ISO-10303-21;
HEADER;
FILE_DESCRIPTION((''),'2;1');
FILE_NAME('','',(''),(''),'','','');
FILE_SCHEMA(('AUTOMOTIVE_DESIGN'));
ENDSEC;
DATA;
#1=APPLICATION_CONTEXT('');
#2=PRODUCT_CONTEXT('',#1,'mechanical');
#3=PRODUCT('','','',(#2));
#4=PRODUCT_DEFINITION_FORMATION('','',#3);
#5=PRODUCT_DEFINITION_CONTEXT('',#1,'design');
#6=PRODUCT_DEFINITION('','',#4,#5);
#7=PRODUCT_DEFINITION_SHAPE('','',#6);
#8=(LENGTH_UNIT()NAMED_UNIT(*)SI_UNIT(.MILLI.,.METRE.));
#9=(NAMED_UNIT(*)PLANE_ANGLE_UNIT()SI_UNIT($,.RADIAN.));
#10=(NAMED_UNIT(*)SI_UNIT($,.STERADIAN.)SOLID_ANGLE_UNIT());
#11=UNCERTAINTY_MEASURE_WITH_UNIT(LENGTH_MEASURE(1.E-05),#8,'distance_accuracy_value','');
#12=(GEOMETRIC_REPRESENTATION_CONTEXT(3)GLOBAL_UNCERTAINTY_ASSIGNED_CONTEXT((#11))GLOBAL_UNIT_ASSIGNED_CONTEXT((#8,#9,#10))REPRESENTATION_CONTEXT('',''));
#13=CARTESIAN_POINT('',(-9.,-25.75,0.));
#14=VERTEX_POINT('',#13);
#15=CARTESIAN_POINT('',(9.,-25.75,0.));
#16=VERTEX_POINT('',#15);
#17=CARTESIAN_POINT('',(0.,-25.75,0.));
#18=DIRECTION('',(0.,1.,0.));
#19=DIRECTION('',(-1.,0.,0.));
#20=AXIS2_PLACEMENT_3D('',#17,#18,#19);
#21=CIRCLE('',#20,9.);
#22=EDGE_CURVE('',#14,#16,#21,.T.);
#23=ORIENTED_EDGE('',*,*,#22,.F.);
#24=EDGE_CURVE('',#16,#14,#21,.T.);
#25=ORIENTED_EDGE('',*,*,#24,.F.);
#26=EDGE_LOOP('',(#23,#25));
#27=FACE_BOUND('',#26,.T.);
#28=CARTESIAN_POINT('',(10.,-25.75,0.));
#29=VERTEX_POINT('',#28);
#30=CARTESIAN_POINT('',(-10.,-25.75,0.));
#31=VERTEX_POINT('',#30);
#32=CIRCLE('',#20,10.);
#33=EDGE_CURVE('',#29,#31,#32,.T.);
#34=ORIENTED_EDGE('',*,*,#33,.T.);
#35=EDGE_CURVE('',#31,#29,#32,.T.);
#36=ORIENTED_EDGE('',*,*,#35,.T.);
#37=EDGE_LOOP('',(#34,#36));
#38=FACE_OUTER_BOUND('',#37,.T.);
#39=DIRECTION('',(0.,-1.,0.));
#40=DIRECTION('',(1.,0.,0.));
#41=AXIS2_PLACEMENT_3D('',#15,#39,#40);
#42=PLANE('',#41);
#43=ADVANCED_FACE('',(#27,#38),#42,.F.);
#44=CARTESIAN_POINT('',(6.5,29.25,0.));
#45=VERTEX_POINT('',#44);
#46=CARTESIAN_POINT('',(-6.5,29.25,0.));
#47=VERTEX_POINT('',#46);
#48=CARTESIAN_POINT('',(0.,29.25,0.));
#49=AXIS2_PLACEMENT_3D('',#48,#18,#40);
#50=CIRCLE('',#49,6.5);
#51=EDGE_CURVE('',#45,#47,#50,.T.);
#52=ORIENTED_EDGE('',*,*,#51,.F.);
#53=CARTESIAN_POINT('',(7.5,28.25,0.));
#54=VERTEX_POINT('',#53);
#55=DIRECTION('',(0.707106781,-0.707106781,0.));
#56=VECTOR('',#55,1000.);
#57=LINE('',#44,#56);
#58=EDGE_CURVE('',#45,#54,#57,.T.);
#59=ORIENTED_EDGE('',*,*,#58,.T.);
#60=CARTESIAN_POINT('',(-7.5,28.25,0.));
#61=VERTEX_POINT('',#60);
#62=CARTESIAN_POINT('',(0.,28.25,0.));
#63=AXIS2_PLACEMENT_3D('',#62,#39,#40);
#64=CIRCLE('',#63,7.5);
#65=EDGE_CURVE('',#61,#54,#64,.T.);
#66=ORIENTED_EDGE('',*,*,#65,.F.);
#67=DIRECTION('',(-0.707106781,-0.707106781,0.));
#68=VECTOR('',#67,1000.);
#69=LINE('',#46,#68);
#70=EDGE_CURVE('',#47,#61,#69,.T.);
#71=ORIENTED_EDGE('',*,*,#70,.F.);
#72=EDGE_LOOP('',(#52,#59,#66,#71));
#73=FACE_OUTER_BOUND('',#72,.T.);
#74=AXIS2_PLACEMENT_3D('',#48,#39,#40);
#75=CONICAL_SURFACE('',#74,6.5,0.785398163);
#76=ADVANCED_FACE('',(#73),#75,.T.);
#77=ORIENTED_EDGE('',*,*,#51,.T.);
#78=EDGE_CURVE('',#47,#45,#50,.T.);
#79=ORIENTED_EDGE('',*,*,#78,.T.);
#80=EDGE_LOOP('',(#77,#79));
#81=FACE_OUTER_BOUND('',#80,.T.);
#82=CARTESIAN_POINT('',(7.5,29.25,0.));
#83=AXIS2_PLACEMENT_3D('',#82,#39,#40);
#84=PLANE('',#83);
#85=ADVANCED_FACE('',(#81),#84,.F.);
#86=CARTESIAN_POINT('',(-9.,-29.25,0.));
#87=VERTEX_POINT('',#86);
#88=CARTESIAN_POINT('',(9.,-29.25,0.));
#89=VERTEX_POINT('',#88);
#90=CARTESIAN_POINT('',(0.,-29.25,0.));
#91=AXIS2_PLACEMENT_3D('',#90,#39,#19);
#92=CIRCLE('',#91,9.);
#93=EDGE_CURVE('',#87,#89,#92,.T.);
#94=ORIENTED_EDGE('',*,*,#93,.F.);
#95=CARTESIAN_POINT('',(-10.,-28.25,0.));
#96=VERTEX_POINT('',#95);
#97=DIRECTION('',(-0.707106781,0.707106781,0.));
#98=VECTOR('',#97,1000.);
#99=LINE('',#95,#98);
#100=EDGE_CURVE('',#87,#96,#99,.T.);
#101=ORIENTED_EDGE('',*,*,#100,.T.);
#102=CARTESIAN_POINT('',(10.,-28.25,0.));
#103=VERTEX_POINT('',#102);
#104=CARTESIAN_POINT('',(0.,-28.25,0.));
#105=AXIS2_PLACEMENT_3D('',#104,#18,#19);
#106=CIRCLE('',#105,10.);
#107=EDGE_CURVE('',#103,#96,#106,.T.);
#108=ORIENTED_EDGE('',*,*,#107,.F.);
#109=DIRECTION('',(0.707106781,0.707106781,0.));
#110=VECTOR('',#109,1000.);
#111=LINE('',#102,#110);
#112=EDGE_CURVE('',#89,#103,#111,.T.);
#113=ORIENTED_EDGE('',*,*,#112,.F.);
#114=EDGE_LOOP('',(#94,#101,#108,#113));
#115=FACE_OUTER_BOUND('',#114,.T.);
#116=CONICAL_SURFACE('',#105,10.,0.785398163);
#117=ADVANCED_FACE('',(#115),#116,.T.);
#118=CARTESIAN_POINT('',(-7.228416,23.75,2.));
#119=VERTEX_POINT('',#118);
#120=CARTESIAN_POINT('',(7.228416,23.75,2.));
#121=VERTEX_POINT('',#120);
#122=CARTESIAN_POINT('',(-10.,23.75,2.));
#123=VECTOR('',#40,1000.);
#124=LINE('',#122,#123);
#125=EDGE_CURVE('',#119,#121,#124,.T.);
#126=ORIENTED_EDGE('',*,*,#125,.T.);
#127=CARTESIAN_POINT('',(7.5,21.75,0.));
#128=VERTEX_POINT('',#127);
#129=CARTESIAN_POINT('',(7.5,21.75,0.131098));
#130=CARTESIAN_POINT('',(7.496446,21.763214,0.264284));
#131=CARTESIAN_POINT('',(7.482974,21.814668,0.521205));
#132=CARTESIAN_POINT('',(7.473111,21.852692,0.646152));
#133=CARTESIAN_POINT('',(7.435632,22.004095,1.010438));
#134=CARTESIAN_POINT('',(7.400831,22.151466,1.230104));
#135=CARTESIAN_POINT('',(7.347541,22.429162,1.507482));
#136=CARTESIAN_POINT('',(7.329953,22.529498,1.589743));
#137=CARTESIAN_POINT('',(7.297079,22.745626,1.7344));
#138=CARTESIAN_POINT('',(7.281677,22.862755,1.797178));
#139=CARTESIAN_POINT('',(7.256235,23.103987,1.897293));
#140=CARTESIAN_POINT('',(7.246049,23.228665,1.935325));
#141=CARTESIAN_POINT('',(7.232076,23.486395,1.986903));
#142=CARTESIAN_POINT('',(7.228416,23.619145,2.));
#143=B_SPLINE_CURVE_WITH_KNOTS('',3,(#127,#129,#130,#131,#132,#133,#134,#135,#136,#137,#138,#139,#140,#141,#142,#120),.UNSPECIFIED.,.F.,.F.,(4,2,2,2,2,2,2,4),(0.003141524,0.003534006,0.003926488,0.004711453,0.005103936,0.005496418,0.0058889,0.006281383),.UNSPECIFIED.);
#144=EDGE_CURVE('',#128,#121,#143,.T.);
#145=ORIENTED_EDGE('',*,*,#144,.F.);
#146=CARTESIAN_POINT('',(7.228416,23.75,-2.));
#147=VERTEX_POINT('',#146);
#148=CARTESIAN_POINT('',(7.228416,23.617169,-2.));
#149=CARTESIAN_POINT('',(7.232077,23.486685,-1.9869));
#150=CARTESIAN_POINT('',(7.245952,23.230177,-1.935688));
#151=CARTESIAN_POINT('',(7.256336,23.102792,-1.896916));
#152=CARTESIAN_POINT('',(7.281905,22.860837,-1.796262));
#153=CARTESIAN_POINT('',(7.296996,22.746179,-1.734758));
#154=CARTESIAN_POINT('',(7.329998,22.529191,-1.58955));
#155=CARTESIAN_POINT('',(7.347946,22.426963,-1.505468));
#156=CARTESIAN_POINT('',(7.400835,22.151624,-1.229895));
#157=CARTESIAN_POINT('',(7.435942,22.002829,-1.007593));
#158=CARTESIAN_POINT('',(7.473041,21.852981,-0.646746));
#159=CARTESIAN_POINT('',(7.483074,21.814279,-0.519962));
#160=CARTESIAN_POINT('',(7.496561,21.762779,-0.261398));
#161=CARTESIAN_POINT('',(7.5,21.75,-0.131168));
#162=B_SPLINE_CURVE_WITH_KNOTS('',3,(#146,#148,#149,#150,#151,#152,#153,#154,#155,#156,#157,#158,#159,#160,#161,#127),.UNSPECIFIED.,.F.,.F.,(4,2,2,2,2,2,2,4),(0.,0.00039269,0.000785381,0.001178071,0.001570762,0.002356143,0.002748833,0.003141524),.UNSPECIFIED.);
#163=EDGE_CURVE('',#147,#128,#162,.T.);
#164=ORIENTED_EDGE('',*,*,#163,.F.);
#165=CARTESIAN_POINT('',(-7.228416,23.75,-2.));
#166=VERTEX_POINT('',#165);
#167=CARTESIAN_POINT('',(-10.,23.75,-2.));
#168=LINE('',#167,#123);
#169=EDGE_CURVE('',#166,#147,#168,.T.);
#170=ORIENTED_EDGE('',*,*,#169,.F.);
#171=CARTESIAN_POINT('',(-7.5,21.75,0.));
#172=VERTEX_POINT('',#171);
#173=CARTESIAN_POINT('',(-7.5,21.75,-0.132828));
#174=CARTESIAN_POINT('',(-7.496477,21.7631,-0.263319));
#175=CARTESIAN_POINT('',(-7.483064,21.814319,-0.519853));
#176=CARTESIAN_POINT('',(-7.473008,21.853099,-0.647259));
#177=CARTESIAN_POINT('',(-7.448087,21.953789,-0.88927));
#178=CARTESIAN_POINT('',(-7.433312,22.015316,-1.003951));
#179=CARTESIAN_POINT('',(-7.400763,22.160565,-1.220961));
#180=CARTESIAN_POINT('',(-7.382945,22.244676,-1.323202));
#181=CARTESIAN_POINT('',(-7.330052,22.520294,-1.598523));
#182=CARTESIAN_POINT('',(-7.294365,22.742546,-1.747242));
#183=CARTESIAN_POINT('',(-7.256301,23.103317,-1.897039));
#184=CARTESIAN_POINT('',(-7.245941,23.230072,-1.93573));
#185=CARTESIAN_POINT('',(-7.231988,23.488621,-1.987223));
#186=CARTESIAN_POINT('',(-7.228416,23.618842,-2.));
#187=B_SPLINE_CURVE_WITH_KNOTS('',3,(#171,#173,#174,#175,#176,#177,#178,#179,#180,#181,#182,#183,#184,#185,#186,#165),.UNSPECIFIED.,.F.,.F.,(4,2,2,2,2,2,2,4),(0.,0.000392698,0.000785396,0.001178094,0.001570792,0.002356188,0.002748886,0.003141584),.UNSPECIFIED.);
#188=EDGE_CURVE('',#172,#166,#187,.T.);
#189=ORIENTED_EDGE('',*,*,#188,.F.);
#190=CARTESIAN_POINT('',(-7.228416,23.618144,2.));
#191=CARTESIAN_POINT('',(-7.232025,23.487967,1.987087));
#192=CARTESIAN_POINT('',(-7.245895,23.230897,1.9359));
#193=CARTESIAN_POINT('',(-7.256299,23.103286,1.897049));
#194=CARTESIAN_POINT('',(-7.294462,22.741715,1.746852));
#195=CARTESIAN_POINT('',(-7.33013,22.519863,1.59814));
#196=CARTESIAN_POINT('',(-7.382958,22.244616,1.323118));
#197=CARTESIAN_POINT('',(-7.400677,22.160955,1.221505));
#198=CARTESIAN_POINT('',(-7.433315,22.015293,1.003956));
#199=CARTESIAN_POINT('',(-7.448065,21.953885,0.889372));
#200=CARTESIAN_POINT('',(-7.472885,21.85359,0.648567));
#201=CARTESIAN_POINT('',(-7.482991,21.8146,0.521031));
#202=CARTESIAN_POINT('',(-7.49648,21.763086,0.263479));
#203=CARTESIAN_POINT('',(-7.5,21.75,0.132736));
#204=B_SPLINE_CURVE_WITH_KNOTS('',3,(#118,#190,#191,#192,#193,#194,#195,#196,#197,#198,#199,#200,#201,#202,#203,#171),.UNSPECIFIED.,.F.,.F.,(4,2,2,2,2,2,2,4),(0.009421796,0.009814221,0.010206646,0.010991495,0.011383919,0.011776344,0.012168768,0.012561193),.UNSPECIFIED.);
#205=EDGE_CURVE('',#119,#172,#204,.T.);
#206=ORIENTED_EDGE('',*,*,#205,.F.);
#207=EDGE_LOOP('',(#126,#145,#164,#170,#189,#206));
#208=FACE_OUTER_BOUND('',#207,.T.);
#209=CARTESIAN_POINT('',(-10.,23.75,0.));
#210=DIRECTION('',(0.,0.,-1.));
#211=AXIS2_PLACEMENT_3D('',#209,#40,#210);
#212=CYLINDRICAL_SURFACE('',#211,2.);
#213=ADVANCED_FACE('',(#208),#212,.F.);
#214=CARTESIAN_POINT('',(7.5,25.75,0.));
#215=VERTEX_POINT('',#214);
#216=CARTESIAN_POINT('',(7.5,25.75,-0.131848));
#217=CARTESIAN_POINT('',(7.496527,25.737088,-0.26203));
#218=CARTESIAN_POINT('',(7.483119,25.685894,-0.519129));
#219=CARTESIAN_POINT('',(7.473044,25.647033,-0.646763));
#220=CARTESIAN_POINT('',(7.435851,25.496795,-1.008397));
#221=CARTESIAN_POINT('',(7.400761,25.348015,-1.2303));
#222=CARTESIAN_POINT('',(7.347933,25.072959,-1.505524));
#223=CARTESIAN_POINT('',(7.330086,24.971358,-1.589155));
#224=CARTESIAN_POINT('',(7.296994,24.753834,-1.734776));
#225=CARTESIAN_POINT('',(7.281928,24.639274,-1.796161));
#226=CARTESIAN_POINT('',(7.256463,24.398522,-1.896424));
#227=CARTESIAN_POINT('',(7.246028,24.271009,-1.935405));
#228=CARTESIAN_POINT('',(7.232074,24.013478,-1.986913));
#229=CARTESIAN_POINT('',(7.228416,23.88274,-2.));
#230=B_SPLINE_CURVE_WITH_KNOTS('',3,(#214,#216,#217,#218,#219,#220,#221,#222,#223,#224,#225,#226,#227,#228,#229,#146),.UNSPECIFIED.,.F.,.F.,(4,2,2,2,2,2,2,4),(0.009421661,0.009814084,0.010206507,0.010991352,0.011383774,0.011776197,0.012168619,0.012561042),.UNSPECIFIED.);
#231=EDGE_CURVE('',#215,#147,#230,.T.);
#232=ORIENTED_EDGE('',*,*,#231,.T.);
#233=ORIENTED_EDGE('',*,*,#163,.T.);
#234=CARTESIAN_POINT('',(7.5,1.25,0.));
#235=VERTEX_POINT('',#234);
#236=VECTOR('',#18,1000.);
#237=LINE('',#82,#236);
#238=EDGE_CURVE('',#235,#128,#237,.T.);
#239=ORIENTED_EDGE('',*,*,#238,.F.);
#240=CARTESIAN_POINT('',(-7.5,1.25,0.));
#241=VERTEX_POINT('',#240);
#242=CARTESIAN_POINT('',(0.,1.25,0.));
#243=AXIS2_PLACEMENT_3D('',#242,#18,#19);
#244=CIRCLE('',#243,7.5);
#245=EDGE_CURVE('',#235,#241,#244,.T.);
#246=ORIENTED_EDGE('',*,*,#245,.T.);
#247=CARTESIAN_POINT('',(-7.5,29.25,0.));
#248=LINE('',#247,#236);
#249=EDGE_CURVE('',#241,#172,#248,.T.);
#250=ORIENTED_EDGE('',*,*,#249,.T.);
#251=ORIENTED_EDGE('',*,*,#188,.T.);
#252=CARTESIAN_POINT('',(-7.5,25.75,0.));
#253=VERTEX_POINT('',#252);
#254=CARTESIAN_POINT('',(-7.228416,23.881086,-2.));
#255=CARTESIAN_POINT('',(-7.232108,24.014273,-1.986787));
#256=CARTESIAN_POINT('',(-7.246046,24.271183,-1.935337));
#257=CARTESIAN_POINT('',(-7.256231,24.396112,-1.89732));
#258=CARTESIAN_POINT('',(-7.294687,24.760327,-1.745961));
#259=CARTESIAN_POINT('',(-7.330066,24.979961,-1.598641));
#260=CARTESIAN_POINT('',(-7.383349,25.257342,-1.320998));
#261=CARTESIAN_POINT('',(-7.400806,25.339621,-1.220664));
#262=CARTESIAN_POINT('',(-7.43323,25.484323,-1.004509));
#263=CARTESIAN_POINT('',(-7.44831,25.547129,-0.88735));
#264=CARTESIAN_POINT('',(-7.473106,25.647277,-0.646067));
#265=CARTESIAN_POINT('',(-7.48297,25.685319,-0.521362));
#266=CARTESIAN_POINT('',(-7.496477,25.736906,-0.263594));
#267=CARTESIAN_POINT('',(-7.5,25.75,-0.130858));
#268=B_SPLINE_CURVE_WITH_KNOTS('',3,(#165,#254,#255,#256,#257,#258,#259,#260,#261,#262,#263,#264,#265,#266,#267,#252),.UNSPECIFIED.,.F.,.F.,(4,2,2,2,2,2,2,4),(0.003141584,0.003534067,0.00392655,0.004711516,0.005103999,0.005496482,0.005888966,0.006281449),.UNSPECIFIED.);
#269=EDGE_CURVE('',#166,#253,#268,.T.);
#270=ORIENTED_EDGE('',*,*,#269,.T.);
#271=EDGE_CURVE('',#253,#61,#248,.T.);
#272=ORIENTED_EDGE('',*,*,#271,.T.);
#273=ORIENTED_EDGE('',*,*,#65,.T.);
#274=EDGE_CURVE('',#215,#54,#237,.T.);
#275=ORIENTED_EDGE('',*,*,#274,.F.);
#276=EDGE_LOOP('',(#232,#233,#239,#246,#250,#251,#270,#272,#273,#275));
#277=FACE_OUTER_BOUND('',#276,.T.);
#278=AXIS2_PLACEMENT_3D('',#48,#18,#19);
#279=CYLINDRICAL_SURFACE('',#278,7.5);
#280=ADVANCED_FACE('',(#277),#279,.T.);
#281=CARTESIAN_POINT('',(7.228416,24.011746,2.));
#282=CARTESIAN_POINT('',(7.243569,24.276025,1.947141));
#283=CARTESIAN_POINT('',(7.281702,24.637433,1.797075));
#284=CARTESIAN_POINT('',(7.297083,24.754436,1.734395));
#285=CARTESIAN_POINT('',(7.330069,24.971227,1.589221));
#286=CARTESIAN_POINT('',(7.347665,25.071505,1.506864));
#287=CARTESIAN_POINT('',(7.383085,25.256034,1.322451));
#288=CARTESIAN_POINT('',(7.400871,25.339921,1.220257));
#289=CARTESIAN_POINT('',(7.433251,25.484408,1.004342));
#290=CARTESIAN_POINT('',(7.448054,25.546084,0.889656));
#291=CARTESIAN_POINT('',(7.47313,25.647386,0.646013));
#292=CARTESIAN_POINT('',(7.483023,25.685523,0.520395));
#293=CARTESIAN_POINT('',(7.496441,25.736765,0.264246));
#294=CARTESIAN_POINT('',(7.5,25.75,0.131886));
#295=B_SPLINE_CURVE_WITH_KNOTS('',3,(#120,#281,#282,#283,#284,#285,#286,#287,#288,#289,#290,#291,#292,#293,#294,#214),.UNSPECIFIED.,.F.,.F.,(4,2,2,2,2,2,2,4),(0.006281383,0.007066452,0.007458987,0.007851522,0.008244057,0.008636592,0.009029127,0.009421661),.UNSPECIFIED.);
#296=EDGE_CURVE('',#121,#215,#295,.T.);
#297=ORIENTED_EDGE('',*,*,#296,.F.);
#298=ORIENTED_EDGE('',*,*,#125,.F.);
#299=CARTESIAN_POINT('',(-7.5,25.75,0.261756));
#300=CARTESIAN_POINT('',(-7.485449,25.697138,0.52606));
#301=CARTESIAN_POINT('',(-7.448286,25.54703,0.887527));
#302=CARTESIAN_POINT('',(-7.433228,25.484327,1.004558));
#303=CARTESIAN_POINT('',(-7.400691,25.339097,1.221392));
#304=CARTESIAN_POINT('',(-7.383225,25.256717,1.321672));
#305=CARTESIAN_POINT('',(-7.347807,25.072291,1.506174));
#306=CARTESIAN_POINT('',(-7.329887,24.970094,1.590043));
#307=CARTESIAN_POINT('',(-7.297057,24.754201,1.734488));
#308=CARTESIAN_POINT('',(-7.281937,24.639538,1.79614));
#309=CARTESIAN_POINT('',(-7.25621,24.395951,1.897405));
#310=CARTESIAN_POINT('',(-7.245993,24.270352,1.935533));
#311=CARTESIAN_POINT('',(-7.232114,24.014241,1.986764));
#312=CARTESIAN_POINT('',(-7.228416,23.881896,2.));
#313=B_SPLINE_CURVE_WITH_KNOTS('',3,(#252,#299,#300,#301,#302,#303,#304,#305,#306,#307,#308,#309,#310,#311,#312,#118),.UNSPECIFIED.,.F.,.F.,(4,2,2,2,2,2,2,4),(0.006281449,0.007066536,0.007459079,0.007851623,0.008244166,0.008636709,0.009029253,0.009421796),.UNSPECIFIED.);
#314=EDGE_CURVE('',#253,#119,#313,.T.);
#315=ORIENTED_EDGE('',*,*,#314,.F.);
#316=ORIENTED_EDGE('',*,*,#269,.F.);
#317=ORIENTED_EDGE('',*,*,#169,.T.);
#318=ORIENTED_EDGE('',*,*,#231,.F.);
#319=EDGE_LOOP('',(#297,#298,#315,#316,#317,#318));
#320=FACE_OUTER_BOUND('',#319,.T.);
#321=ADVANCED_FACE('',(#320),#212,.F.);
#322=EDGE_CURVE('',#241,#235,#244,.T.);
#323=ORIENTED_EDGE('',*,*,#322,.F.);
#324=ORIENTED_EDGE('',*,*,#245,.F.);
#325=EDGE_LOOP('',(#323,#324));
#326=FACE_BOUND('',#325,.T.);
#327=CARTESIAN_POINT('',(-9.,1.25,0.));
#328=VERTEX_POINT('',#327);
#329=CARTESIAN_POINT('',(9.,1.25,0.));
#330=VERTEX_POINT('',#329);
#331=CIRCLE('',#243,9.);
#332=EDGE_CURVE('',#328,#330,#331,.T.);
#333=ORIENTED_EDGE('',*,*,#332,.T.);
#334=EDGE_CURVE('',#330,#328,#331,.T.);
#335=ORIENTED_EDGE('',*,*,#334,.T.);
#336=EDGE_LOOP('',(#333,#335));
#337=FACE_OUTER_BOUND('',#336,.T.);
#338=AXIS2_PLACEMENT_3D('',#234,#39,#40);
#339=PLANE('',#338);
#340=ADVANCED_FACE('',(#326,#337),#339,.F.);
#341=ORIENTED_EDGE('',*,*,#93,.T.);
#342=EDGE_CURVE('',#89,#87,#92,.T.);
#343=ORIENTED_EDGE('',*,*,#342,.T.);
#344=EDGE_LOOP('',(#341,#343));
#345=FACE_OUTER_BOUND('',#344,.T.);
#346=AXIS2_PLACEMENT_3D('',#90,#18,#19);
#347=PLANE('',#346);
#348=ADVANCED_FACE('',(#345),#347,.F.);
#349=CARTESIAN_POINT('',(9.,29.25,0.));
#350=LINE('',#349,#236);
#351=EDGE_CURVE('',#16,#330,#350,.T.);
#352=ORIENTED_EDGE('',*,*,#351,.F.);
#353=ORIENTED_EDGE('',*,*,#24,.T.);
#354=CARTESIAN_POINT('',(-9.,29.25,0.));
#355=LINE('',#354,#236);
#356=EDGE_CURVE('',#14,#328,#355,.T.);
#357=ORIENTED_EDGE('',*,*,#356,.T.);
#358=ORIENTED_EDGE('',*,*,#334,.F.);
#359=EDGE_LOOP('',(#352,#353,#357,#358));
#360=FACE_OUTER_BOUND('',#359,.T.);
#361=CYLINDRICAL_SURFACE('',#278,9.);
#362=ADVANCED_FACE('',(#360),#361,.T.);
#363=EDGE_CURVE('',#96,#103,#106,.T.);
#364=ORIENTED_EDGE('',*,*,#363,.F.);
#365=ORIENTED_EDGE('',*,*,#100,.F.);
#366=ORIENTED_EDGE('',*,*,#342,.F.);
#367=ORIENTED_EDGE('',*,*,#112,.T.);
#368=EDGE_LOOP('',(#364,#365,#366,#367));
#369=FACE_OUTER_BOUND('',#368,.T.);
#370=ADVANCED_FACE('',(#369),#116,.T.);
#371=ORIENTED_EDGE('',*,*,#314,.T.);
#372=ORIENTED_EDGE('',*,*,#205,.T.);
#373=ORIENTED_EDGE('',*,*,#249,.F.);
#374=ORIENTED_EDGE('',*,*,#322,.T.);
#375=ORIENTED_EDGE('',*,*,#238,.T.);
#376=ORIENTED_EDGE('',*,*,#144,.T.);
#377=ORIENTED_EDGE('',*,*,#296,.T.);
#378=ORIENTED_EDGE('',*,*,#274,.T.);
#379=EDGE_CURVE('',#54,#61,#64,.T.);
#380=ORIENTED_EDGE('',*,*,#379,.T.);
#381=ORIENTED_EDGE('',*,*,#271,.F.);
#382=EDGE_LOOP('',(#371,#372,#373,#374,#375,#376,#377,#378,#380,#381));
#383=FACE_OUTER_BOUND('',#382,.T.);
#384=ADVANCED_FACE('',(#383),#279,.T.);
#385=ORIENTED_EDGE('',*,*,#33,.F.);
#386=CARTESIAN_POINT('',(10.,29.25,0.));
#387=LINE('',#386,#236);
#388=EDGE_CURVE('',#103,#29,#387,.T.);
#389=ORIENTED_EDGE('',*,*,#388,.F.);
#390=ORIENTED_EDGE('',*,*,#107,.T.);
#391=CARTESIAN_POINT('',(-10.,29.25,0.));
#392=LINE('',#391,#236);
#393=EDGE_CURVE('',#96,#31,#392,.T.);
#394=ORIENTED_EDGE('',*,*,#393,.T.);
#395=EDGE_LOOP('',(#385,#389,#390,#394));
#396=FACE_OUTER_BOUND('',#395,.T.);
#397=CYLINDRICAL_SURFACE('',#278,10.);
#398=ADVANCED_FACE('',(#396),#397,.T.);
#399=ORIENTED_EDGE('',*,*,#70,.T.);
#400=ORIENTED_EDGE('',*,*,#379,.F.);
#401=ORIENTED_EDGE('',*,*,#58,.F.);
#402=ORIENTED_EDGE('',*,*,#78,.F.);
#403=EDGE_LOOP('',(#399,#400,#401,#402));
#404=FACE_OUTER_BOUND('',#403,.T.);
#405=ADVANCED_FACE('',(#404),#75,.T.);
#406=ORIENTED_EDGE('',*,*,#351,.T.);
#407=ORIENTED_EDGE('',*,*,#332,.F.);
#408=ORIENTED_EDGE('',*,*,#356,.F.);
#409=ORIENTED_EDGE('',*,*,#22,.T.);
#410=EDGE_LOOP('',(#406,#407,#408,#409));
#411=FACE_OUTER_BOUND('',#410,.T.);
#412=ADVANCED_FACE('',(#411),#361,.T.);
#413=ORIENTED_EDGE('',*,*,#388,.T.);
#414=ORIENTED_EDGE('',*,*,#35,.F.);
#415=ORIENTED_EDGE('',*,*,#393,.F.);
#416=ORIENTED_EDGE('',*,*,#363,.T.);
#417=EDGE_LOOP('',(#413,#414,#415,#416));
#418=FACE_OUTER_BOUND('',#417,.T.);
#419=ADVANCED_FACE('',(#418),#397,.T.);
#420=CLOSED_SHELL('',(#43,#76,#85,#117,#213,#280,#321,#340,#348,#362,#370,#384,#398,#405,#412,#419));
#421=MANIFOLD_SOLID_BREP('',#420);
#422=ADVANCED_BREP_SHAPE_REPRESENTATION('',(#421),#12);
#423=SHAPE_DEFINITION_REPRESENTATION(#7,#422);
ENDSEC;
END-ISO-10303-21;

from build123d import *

# Parameters (mm, degrees)
SKETCH_2_R          = 2
CUT_EXTRUDE_1_DEPTH = 10
CHAMFER_1_SIZE      = 1


with BuildPart() as part:
    # 草图1 → 旋转1 (revolve)
    with BuildSketch(Plane.XY, mode=Mode.PRIVATE) as revolve_1_sk:
        Polygon((0, 29.25), (0, -29.25), (10, -29.25), (10, -25.75), (9, -25.75), (9, 1.25), (7.5, 1.25), (7.5, 29.25), align=None)
    revolve(revolve_1_sk.sketch.rotate(Axis((0, 29.25, 0), (0, -1, 0)), 180), axis=Axis((0, 29.25, 0), (0, -1, 0)))

    # 草图2 → 切除-拉伸1 (cut, symmetric)
    with BuildSketch(Plane(origin=(0, 0, 0), x_dir=(0, 0, -1), z_dir=(1, 0, 0))):
        with Locations((0, 23.75)):
            Circle(SKETCH_2_R)
    extrude(amount=CUT_EXTRUDE_1_DEPTH, both=True, mode=Mode.SUBTRACT)

    # 倒角1
    chamfer_1_edges = [part.edges().sort_by_distance(p)[0] for p in [
        (10, -29.25, 0),
        (7.5, 29.25, 0),
    ]]
    chamfer(chamfer_1_edges, length=CHAMFER_1_SIZE)


solid = part.part
